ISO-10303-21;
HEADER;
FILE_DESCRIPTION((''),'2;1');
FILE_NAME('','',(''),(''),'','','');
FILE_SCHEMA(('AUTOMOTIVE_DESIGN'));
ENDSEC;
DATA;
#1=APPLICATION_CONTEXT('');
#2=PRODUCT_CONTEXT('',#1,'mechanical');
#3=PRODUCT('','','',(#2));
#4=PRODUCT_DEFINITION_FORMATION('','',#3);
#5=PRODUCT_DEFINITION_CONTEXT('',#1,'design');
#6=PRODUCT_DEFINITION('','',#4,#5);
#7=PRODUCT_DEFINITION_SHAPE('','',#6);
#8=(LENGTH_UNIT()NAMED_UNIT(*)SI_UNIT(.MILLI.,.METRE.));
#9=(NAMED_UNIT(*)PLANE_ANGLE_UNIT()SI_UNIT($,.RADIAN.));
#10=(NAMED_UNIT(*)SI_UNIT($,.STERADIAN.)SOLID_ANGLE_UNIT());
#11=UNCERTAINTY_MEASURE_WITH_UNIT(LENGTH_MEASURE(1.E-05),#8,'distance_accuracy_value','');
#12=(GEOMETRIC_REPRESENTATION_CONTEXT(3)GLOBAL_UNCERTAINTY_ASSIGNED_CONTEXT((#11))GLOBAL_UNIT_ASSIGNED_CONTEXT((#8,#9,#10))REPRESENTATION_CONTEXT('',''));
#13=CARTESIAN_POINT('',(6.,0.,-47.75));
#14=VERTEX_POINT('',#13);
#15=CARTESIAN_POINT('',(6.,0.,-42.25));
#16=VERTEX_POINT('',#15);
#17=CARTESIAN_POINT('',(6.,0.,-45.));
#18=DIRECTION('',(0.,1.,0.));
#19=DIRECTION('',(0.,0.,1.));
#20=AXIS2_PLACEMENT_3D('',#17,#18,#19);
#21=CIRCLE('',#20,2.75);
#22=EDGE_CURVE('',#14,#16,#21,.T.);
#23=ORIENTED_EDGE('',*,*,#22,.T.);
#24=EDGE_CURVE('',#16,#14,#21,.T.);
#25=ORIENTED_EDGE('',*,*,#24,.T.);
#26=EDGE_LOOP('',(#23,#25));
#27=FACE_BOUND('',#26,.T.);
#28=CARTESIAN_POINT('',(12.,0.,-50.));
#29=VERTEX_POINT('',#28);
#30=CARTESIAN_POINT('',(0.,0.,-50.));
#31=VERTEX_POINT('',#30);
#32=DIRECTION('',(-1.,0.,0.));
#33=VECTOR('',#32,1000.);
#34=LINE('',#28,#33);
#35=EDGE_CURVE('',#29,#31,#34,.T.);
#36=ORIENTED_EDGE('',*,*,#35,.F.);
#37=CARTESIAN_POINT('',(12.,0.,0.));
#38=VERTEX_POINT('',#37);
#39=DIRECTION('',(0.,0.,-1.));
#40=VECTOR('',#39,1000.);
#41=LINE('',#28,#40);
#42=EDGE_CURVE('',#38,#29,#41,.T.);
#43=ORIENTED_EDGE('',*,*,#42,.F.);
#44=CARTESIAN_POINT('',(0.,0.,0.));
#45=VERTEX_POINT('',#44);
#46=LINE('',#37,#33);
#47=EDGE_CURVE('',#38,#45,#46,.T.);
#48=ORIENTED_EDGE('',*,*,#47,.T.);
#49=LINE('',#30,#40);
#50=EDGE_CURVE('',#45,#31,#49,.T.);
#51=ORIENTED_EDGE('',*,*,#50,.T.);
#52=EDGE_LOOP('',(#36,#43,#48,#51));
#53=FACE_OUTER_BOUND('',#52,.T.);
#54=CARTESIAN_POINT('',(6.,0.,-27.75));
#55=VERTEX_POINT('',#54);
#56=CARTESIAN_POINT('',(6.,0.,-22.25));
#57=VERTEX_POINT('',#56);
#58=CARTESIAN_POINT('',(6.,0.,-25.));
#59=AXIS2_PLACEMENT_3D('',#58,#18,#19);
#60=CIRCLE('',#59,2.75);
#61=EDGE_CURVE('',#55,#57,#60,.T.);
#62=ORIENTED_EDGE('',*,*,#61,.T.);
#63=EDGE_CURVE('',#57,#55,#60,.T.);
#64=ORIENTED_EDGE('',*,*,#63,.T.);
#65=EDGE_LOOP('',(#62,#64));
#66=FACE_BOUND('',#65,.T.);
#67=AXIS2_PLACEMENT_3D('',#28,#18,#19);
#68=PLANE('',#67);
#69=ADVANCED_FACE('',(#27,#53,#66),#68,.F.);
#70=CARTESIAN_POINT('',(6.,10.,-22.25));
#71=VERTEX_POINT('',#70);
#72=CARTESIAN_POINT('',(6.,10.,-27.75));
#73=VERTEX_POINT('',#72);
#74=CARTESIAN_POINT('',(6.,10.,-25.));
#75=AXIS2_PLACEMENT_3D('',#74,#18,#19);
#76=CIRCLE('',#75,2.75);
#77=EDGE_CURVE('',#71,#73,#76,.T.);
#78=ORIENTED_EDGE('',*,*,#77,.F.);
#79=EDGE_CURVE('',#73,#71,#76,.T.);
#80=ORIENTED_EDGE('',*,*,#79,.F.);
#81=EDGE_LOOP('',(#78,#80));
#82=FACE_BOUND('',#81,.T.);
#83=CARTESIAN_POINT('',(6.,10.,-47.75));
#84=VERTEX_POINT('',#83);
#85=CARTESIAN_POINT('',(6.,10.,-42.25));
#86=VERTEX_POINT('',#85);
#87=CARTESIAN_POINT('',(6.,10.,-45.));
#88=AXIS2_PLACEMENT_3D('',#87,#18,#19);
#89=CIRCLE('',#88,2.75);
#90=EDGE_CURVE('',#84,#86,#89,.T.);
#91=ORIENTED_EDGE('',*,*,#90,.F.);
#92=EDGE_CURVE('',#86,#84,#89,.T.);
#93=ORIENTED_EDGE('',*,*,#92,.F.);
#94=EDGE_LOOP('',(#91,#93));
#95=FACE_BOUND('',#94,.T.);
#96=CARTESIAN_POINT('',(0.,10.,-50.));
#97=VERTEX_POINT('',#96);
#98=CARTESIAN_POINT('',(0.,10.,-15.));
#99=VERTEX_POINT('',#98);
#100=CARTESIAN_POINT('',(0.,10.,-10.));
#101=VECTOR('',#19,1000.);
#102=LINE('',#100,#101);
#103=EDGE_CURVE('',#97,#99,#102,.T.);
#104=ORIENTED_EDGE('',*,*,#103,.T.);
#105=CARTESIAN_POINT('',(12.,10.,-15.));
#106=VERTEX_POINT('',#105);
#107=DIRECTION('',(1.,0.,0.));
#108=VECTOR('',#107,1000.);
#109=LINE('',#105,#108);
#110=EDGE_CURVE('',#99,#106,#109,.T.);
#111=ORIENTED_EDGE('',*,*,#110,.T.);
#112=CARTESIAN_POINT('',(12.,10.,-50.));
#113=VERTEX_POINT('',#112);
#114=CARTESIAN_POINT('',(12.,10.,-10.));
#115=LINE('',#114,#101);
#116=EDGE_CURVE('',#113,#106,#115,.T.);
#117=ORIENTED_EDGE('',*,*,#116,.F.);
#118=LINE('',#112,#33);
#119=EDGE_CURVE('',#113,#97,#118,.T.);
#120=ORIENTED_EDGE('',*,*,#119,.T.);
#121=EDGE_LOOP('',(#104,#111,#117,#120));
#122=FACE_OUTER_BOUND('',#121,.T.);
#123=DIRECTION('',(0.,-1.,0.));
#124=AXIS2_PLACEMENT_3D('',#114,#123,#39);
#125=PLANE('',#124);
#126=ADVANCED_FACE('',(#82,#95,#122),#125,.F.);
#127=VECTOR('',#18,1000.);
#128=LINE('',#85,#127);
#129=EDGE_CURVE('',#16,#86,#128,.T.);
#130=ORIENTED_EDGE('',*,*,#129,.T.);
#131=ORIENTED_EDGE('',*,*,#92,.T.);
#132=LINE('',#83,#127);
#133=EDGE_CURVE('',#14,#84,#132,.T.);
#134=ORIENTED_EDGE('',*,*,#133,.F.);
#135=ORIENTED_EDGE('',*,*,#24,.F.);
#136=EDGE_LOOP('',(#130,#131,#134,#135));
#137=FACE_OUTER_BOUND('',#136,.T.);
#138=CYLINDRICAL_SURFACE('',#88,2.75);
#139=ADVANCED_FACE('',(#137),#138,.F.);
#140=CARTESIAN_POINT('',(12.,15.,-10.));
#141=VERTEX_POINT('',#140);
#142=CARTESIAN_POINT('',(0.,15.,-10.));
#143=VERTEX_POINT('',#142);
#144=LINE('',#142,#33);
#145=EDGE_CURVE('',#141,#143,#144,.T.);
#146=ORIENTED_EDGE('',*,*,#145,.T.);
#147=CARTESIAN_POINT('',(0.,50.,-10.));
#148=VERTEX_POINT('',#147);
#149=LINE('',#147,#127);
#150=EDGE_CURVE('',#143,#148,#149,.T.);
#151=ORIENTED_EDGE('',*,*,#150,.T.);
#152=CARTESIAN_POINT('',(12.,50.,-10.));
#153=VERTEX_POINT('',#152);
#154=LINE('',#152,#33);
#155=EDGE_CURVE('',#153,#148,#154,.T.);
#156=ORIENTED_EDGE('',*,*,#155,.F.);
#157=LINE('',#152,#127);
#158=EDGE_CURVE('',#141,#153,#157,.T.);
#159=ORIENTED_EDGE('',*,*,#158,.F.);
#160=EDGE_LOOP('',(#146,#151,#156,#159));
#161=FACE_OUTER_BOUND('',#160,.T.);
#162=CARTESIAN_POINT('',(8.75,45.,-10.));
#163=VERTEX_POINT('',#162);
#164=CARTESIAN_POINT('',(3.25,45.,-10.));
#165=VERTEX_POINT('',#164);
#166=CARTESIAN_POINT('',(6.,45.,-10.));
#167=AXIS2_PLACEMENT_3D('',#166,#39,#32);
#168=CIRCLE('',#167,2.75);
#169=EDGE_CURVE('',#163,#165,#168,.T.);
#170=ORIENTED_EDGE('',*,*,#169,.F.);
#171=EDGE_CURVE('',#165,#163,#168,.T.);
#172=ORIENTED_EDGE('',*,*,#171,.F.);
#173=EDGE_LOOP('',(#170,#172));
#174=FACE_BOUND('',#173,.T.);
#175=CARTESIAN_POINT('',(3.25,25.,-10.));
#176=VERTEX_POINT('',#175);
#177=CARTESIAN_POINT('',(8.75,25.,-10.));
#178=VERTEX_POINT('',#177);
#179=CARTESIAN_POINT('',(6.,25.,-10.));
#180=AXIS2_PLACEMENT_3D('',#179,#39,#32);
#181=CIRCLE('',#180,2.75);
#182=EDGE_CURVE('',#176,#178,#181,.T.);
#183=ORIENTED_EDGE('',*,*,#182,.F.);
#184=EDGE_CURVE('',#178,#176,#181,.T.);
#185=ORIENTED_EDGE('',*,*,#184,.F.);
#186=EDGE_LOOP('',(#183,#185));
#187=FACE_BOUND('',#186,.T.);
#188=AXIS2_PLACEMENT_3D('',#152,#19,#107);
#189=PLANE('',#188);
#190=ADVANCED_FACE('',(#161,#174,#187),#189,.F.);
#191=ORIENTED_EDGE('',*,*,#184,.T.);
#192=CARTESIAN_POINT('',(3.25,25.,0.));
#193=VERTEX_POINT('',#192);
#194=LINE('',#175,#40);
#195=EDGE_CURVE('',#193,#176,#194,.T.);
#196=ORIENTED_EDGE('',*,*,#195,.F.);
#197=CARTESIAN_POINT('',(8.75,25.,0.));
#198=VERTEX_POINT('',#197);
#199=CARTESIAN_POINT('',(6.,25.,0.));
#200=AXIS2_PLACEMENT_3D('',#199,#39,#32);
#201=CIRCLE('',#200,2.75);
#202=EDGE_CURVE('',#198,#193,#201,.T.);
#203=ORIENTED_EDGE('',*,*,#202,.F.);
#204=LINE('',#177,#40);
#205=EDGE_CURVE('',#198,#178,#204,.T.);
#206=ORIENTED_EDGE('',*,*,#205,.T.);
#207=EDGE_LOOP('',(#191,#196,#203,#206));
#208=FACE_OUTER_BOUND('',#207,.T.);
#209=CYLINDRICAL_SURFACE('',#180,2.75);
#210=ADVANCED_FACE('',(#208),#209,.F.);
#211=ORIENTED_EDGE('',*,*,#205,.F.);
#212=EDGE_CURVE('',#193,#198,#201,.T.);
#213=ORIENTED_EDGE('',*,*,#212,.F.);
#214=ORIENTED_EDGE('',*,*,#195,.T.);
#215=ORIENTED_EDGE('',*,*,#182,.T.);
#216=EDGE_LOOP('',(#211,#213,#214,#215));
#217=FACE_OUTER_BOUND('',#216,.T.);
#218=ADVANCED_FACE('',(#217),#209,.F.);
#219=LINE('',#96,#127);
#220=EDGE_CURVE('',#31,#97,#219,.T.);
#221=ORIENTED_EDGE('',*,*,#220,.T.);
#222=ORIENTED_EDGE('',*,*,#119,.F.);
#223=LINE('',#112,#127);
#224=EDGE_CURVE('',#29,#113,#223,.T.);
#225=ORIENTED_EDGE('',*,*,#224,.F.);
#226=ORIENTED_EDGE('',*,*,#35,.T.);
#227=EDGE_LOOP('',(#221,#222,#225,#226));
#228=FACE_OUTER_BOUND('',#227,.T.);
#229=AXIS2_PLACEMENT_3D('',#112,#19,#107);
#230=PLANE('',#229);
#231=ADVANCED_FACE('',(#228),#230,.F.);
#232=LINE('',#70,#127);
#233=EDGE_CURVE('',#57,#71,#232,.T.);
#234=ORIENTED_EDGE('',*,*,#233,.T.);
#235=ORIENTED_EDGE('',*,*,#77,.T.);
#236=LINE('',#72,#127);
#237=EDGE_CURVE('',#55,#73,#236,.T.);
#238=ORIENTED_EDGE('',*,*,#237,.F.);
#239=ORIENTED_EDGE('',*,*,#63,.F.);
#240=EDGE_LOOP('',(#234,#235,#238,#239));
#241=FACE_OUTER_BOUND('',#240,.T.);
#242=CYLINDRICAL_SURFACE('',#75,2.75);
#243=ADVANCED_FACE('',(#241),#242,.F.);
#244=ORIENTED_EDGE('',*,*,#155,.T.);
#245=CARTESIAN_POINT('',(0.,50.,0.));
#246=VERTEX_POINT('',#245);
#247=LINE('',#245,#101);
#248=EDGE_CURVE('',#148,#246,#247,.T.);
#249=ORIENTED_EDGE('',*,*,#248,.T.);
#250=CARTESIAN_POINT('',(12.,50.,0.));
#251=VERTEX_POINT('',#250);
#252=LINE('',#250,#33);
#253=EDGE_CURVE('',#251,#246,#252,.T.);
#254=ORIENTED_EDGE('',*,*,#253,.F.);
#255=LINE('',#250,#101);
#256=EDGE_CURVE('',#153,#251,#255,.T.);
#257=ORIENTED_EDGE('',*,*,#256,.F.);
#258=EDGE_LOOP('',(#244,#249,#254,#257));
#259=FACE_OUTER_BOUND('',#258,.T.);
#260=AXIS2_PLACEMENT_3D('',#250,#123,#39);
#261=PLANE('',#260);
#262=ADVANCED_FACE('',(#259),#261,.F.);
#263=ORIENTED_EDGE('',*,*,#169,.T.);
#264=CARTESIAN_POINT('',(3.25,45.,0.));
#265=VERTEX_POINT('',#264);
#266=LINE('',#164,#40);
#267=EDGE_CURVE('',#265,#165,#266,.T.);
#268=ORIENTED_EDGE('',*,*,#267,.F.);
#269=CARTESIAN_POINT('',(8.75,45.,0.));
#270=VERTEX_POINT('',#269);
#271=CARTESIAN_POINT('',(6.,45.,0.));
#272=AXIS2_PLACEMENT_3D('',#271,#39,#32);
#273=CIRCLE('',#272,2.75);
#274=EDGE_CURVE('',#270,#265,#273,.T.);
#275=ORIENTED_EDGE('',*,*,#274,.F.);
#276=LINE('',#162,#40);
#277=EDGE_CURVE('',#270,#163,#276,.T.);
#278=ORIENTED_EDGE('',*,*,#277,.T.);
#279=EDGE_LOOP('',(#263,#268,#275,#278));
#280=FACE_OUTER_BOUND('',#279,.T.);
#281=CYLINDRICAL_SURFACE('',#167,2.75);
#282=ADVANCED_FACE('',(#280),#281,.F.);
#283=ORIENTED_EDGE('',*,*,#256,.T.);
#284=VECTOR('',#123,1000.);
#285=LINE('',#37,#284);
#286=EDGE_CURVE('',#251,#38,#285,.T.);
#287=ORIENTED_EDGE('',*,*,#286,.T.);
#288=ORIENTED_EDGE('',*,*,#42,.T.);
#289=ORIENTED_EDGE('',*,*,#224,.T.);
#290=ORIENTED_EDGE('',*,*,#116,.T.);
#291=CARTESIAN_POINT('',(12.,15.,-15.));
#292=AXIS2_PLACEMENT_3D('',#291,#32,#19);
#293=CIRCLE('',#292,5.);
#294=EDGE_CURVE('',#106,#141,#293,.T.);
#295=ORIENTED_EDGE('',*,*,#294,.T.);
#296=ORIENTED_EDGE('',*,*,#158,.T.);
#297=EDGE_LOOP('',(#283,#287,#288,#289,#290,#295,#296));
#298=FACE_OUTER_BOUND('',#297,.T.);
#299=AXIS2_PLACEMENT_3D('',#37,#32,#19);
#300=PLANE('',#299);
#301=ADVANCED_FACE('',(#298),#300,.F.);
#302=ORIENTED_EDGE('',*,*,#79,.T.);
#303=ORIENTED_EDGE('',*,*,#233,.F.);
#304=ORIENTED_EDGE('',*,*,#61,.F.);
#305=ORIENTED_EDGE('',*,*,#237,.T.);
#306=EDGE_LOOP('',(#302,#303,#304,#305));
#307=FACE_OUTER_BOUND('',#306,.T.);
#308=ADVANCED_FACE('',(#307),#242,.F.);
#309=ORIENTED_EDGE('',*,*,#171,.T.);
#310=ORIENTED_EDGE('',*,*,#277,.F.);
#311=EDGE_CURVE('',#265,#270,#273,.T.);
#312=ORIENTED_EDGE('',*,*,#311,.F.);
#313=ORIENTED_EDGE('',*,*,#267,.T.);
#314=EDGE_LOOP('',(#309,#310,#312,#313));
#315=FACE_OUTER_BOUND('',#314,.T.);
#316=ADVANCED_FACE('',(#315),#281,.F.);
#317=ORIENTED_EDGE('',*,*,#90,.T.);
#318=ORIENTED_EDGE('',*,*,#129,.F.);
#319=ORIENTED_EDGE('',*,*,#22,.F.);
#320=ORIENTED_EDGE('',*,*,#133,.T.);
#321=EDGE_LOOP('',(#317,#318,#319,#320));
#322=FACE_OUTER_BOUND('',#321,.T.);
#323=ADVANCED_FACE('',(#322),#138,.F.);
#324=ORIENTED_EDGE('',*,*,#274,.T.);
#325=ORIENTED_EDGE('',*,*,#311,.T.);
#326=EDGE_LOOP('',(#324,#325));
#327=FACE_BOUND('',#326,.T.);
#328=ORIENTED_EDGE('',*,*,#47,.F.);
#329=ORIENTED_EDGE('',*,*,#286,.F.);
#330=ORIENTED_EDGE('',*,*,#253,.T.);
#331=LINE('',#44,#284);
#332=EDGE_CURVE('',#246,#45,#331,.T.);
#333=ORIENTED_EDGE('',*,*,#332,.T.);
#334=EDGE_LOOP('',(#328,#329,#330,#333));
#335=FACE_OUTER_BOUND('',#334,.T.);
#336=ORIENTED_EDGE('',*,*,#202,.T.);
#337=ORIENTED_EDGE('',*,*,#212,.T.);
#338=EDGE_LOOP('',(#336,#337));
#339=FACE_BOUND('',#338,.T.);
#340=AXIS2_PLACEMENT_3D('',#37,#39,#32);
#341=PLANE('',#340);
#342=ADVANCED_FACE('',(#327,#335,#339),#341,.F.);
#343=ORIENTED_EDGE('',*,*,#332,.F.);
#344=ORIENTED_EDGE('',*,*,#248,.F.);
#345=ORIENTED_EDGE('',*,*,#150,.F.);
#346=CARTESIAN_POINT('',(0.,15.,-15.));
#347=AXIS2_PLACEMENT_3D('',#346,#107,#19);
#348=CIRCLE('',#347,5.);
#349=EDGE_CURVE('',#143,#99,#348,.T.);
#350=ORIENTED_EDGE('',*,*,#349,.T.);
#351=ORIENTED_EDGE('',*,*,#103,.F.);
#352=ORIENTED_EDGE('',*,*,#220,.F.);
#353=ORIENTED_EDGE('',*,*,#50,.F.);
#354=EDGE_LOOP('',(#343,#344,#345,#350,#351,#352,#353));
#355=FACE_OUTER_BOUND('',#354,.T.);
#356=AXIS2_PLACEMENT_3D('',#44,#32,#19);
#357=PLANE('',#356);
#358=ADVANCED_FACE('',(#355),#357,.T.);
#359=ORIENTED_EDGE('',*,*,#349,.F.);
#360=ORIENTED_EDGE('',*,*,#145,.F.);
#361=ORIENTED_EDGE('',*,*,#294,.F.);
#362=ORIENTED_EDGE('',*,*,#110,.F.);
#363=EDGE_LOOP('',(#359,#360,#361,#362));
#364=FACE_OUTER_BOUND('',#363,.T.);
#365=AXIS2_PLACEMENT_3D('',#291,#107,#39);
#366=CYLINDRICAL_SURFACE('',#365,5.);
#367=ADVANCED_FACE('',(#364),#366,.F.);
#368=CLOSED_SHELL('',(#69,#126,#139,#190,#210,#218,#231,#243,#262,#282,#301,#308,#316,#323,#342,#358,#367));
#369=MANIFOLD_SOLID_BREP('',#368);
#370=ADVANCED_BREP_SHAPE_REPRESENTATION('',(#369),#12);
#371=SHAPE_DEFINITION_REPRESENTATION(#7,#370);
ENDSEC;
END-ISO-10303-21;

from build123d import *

# Parameters (mm, degrees)
BOSS_EXTRUDE1_DEPTH  = 12
FILLET1_R            = 5
M5_CLEARANCE_HOLE1_D = 5.5
M5_CLEARANCE_HOLE2_D = 5.5


with BuildPart() as part:
    # Sketch1 → Boss-Extrude1 (new body)
    with BuildSketch(Plane(origin=(0, 0, 0), x_dir=(0, 0, -1), z_dir=(1, 0, 0))):
        Polygon((0, 0), (0, 50), (10, 50), (10, 10), (50, 10), (50, 0), align=None)
    extrude(amount=BOSS_EXTRUDE1_DEPTH)

    # Fillet1
    fillet1_edges = [part.edges().sort_by_distance(p)[0] for p in [
        (6, 10, -10),
    ]]
    fillet(fillet1_edges, radius=FILLET1_R)

    # M5 Clearance Hole1 (through all)
    with Locations(Plane(origin=(0, 0, -10), x_dir=(-1, 0, 0), z_dir=(0, 0, -1))):
        with Locations((-6, 25), (-6, 45)):
            Hole(M5_CLEARANCE_HOLE1_D / 2)

    # M5 Clearance Hole2 (through all)
    with Locations(Plane(origin=(0, 10, 0), x_dir=(1, 0, 0), z_dir=(0, 1, 0))):
        with Locations((6, 45), (6, 25)):
            Hole(M5_CLEARANCE_HOLE2_D / 2)


solid = part.part
